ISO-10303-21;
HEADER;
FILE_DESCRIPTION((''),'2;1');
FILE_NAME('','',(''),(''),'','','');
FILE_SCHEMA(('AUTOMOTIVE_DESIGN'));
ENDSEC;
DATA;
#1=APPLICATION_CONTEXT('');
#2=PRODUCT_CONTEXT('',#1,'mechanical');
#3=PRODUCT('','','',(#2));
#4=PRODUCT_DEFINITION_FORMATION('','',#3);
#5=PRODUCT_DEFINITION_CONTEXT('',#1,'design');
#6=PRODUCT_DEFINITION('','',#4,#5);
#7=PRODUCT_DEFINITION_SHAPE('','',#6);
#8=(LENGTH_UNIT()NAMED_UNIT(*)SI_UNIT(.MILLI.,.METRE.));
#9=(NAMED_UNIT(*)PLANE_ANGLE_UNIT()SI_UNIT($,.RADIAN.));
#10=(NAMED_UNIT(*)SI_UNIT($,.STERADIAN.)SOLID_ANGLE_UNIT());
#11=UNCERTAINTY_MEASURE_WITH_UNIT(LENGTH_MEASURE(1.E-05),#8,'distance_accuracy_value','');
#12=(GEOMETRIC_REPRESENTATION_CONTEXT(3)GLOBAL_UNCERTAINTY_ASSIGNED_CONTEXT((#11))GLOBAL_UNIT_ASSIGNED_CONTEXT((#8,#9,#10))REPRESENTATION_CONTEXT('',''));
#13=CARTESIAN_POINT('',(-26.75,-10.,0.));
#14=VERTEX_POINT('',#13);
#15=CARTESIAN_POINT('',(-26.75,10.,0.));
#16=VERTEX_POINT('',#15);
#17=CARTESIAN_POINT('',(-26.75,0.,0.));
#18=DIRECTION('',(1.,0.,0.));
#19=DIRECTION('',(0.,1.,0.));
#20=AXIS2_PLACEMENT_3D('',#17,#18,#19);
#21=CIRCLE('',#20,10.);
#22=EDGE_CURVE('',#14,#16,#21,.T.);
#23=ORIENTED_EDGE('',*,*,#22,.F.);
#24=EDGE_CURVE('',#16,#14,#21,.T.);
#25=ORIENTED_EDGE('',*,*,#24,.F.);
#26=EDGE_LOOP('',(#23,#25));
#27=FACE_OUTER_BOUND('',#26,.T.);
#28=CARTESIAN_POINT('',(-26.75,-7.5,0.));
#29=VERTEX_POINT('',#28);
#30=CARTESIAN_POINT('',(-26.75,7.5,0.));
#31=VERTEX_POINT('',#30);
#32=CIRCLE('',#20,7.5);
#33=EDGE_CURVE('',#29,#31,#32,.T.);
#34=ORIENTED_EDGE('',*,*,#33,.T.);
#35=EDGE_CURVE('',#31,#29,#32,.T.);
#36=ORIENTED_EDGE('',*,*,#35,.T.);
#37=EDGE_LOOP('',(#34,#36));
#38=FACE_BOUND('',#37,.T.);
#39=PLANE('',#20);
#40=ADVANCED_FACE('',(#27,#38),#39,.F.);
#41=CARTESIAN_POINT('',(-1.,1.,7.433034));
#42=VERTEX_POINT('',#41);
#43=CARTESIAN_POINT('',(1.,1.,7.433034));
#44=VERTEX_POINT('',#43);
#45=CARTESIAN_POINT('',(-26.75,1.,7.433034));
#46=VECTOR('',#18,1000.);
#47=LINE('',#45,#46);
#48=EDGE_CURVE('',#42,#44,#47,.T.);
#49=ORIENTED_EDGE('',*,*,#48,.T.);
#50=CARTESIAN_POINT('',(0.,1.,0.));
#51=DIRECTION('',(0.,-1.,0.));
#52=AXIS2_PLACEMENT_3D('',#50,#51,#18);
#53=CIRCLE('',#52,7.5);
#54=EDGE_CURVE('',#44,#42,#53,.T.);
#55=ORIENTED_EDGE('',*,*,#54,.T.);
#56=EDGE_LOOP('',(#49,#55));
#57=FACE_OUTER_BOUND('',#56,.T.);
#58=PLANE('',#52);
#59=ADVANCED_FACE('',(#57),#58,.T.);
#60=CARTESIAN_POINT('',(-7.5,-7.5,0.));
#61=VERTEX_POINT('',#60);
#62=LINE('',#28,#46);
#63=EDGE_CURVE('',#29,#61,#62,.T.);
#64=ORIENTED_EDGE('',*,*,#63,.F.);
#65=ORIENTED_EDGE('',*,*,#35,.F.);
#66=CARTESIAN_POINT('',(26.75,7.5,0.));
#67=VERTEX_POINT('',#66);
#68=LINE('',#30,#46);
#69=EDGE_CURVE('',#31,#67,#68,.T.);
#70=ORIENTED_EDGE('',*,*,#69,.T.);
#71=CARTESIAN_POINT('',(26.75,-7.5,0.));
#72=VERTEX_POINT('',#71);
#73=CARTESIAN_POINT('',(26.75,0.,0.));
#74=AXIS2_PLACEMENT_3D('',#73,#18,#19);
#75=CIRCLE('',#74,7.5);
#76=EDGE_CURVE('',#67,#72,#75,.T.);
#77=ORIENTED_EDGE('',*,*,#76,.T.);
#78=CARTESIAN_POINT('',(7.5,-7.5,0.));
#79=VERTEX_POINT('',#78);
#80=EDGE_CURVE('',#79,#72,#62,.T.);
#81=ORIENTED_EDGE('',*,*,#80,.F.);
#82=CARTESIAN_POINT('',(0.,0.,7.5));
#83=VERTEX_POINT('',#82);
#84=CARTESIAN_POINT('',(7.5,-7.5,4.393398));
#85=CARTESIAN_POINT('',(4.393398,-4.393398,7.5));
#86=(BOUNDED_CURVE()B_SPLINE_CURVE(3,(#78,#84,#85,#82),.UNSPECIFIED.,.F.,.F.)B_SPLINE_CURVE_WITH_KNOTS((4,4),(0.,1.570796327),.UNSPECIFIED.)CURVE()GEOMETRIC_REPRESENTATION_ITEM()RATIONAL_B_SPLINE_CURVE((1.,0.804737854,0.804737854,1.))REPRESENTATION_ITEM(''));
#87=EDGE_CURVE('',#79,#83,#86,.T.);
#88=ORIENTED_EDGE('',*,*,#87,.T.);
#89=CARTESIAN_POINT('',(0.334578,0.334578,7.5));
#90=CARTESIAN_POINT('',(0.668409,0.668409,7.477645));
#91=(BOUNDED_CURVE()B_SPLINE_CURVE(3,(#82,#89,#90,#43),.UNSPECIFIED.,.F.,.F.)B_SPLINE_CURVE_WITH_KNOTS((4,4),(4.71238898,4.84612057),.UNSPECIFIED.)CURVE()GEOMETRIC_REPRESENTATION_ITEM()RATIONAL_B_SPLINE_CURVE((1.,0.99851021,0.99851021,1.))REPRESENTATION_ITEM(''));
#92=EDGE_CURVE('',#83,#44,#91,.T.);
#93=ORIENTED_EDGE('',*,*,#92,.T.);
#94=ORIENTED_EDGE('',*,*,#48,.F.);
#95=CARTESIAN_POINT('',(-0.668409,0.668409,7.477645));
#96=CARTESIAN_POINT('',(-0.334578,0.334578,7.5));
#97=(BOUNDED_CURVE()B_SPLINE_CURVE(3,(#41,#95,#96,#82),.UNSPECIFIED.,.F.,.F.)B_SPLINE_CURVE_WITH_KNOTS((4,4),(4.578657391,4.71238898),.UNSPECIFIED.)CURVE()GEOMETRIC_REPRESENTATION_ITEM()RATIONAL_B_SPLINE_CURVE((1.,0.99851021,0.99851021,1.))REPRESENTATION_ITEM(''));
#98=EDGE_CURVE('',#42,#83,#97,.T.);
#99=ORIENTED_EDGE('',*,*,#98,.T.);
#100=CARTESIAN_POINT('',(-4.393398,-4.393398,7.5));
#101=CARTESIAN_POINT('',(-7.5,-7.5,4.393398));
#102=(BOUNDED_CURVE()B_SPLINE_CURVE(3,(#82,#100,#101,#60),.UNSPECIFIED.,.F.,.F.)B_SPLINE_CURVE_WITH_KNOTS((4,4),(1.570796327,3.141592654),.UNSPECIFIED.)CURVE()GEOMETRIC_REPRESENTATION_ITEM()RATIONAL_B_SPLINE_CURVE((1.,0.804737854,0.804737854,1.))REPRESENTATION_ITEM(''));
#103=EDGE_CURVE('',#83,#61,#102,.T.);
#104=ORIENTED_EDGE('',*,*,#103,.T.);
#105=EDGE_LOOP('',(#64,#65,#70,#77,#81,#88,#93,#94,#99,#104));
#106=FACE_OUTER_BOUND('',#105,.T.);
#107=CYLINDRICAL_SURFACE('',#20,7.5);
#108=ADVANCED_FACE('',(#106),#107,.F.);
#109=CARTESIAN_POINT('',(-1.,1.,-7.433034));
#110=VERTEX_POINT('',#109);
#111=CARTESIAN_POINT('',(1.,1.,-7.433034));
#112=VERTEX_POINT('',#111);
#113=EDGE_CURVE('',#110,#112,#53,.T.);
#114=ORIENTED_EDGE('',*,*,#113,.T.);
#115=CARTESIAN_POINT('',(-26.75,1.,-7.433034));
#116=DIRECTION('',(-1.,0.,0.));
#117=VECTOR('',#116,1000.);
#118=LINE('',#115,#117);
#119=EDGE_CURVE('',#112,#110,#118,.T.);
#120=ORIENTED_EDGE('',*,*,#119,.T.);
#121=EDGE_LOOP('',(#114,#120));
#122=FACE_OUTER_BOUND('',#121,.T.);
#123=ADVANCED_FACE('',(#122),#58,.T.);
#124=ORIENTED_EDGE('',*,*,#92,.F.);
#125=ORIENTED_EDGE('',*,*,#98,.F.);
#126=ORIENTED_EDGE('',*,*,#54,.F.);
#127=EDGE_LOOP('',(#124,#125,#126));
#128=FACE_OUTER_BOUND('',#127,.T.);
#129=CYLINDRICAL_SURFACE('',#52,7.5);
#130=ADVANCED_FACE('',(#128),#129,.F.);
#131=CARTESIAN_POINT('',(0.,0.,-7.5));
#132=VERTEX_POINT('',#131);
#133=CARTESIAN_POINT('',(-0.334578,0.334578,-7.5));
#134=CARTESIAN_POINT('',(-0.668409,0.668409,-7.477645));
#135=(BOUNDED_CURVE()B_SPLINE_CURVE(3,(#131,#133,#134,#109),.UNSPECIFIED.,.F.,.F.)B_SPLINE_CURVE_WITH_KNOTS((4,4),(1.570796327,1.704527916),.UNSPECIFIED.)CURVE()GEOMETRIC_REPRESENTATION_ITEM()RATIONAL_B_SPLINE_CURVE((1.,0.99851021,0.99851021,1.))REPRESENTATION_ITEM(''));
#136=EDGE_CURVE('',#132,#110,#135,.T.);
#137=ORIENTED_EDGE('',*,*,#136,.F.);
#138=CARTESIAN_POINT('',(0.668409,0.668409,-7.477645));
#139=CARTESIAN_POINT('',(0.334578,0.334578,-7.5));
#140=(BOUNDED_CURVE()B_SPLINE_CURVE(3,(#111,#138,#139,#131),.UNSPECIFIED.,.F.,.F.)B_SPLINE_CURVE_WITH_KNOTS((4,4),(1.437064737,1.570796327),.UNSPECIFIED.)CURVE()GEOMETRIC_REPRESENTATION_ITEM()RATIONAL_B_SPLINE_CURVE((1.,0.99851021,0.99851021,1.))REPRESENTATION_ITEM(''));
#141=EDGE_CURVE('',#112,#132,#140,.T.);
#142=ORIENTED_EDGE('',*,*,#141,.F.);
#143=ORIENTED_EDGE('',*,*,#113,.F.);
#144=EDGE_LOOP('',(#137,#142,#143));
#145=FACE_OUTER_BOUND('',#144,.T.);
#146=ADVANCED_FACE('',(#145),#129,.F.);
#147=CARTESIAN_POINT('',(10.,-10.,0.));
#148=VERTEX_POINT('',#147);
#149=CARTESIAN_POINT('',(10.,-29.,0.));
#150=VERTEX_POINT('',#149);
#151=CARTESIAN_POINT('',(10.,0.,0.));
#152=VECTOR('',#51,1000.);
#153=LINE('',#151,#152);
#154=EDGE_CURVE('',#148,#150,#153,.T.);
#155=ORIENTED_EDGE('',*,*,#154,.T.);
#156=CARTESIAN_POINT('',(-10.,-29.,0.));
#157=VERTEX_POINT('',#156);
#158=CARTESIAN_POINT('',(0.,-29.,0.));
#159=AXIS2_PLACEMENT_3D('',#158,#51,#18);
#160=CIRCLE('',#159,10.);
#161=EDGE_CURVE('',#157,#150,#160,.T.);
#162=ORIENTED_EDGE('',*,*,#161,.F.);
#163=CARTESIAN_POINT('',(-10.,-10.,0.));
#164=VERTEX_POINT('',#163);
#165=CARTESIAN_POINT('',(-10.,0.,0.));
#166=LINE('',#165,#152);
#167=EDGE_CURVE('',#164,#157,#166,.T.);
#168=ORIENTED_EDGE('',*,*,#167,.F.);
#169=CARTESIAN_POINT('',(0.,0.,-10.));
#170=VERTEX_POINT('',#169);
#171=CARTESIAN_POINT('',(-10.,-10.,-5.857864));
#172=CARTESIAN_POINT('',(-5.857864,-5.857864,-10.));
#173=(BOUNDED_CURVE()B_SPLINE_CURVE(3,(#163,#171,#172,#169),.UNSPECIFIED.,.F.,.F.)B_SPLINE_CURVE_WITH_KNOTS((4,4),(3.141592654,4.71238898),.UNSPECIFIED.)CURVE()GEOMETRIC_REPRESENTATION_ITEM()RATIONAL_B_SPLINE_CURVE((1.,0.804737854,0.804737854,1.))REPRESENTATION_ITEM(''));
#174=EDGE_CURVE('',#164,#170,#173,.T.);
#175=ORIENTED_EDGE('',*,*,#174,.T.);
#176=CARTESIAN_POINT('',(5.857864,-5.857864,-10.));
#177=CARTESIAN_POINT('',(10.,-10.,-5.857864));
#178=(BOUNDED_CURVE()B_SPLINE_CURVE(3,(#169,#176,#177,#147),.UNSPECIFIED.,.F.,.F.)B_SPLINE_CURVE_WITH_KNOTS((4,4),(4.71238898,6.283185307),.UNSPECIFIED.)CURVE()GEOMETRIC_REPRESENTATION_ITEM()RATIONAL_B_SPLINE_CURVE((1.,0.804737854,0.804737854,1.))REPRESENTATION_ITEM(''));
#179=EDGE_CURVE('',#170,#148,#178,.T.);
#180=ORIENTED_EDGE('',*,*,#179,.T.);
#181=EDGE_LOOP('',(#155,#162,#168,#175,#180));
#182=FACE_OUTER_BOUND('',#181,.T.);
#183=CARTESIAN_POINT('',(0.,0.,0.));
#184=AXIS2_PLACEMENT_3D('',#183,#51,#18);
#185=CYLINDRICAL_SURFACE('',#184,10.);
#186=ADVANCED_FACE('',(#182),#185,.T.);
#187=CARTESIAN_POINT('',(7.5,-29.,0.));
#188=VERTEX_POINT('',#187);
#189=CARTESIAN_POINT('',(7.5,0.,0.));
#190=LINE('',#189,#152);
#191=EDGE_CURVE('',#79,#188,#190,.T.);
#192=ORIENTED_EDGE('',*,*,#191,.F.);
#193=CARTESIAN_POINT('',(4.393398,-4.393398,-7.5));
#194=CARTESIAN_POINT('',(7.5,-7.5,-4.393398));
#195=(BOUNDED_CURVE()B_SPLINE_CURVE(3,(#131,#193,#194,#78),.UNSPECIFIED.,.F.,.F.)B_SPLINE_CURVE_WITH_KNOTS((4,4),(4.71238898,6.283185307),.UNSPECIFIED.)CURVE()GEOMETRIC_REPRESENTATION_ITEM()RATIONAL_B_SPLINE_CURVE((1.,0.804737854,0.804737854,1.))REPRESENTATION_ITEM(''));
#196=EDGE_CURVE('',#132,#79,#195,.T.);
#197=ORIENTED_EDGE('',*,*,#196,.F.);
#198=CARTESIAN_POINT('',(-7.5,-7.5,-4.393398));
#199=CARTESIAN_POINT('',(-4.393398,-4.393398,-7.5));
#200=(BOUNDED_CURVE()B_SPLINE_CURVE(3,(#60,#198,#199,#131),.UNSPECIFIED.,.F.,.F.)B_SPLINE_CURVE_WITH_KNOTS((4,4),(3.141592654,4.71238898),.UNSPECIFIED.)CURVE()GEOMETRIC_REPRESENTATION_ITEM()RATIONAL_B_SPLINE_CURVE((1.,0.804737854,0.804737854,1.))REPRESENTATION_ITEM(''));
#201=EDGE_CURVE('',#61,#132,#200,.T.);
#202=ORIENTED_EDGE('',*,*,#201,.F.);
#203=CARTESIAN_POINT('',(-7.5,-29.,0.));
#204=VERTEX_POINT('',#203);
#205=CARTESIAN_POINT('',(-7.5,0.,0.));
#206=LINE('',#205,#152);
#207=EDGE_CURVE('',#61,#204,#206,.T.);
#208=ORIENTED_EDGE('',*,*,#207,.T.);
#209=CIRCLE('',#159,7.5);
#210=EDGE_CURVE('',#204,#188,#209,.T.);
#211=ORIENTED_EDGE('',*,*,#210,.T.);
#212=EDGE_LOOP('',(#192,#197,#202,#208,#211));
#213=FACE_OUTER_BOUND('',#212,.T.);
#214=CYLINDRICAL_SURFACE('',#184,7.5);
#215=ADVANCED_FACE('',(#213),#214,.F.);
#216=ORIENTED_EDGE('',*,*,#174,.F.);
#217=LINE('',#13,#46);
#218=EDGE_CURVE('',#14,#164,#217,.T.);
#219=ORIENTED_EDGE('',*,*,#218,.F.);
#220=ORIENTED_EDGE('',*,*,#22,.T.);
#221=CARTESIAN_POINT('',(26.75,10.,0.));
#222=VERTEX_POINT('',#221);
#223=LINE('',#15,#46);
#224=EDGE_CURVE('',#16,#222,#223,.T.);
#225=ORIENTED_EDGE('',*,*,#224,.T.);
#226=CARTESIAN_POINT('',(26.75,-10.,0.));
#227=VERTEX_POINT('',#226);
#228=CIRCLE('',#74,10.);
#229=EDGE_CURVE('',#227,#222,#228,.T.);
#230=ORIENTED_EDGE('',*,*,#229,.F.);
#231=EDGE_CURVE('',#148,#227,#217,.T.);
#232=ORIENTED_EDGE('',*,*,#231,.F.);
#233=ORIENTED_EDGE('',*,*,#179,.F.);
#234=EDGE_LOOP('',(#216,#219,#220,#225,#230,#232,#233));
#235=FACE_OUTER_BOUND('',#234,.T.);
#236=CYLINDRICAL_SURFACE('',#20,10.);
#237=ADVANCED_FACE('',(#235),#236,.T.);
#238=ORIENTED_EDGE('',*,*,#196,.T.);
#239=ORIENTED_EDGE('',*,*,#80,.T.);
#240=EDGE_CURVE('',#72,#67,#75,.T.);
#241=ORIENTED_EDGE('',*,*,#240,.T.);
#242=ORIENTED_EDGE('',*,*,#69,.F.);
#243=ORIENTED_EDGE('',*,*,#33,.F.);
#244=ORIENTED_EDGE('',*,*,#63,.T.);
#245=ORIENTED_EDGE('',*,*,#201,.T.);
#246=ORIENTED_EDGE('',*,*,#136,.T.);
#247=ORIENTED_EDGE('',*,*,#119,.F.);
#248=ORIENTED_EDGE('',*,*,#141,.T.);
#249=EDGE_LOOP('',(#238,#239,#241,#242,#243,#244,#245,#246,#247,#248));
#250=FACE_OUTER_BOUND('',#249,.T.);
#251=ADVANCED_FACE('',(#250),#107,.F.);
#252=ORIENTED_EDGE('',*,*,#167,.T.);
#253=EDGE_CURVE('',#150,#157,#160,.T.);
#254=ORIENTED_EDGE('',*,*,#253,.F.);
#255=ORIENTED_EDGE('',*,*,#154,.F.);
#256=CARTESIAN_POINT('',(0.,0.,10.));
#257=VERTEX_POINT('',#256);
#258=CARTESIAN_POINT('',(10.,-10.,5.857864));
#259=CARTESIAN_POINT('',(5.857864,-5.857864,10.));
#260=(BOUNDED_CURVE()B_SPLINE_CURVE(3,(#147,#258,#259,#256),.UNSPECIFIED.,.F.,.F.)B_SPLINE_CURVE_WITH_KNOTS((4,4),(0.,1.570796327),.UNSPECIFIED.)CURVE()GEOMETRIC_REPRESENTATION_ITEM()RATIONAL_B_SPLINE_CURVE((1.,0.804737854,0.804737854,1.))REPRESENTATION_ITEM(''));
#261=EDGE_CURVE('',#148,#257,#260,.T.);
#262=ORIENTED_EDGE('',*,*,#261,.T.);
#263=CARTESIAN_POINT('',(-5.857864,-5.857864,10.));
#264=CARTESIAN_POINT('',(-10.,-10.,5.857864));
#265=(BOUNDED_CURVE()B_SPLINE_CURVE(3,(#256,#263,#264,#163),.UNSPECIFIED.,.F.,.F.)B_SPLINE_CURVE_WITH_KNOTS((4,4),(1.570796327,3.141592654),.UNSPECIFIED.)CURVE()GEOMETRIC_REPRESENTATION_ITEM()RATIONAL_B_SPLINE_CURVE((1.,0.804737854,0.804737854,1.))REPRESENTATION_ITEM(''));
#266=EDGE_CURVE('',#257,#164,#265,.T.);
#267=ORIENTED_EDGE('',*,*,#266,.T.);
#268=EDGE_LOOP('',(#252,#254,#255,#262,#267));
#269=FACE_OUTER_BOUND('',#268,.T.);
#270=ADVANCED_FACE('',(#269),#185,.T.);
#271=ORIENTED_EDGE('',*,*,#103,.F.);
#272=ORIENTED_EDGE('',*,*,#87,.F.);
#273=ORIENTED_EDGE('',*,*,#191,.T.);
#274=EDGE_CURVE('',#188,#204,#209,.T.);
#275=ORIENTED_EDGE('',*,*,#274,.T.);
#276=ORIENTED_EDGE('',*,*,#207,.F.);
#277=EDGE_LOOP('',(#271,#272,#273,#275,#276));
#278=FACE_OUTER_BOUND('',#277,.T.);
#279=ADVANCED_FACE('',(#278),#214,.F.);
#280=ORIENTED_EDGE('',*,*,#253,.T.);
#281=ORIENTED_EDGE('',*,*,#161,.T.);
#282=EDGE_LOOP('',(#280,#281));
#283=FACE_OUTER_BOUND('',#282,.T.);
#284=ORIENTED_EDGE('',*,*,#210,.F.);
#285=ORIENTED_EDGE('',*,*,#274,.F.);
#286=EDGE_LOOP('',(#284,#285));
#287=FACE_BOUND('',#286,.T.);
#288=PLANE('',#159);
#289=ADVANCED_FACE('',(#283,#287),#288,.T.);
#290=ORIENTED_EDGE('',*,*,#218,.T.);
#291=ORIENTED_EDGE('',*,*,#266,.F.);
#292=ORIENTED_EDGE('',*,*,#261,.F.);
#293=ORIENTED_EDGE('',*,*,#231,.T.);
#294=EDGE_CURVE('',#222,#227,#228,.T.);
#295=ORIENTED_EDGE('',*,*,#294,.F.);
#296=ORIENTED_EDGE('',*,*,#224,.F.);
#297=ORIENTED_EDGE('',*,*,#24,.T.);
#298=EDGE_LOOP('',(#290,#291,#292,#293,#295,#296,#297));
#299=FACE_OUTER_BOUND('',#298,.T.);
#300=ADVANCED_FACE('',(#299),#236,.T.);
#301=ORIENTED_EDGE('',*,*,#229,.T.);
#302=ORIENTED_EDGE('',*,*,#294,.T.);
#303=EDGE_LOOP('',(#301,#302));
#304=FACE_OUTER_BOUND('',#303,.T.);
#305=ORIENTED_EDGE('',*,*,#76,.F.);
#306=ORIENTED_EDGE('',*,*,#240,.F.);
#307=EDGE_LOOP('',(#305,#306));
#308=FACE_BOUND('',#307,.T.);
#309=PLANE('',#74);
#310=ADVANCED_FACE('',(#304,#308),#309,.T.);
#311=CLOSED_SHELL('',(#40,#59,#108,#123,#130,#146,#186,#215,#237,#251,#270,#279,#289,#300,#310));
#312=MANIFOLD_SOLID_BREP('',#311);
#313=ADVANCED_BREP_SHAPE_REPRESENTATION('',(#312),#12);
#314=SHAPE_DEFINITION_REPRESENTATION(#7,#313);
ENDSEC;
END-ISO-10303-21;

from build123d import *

# Parameters (mm, degrees)
SWEEP_THIN_PART_1_PROFILE_R   = 10
SWEEP_THIN_PART_1_PROFILE_R_2 = 7.5
SWEEP_THIN_PART_2_PROFILE_R   = 10
SWEEP_THIN_PART_2_PROFILE_R_2 = 7.5
SKETCH15_R                    = 7.5
CUT_EXTRUDE1_DEPTH            = 62.67049551
SKETCH18_R                    = 7.5
CUT_EXTRUDE2_DEPTH            = 30


with BuildPart() as part:
    # Sweep-thin part 1: sweep along a path in Sketch1
    with BuildLine(Plane.XY) as sweep_thin_part_1_path:
        Line((-26.75, 0), (26.75, 0))
    # Sweep-thin part 1 profile (on start of the path) → Sweep-thin part 1 (sweep)
    with BuildSketch(Plane.YZ.offset(-26.75)):
        Circle(SWEEP_THIN_PART_1_PROFILE_R)
        Circle(SWEEP_THIN_PART_1_PROFILE_R_2, mode=Mode.SUBTRACT)
    sweep(path=sweep_thin_part_1_path.line)

    # Sweep-thin part 2: sweep along a path in Sketch8
    with BuildLine(Plane.XY) as sweep_thin_part_2_path:
        Line((0, 0), (0, -29))
    # Sweep-thin part 2 profile (on start of the path) → Sweep-thin part 2 (sweep)
    with BuildSketch(Plane(origin=(0, 0, 0), x_dir=(-1, 0, 0), z_dir=(0, -1, 0))):
        Circle(SWEEP_THIN_PART_2_PROFILE_R)
        Circle(SWEEP_THIN_PART_2_PROFILE_R_2, mode=Mode.SUBTRACT)
    sweep(path=sweep_thin_part_2_path.line)

    # Sketch15 → Cut-Extrude1 (cut, through all)
    with BuildSketch(Plane.ZY.offset(26.75)):
        with Locations(Location((0, 0, 0), (0, 0, 90))):
            Circle(SKETCH15_R)
    extrude(amount=-CUT_EXTRUDE1_DEPTH, mode=Mode.SUBTRACT)

    # Sketch18 → Cut-Extrude2 (cut)
    with BuildSketch(Plane.XZ.offset(29)):
        Circle(SKETCH18_R)
    extrude(amount=-CUT_EXTRUDE2_DEPTH, mode=Mode.SUBTRACT)


solid = part.part
